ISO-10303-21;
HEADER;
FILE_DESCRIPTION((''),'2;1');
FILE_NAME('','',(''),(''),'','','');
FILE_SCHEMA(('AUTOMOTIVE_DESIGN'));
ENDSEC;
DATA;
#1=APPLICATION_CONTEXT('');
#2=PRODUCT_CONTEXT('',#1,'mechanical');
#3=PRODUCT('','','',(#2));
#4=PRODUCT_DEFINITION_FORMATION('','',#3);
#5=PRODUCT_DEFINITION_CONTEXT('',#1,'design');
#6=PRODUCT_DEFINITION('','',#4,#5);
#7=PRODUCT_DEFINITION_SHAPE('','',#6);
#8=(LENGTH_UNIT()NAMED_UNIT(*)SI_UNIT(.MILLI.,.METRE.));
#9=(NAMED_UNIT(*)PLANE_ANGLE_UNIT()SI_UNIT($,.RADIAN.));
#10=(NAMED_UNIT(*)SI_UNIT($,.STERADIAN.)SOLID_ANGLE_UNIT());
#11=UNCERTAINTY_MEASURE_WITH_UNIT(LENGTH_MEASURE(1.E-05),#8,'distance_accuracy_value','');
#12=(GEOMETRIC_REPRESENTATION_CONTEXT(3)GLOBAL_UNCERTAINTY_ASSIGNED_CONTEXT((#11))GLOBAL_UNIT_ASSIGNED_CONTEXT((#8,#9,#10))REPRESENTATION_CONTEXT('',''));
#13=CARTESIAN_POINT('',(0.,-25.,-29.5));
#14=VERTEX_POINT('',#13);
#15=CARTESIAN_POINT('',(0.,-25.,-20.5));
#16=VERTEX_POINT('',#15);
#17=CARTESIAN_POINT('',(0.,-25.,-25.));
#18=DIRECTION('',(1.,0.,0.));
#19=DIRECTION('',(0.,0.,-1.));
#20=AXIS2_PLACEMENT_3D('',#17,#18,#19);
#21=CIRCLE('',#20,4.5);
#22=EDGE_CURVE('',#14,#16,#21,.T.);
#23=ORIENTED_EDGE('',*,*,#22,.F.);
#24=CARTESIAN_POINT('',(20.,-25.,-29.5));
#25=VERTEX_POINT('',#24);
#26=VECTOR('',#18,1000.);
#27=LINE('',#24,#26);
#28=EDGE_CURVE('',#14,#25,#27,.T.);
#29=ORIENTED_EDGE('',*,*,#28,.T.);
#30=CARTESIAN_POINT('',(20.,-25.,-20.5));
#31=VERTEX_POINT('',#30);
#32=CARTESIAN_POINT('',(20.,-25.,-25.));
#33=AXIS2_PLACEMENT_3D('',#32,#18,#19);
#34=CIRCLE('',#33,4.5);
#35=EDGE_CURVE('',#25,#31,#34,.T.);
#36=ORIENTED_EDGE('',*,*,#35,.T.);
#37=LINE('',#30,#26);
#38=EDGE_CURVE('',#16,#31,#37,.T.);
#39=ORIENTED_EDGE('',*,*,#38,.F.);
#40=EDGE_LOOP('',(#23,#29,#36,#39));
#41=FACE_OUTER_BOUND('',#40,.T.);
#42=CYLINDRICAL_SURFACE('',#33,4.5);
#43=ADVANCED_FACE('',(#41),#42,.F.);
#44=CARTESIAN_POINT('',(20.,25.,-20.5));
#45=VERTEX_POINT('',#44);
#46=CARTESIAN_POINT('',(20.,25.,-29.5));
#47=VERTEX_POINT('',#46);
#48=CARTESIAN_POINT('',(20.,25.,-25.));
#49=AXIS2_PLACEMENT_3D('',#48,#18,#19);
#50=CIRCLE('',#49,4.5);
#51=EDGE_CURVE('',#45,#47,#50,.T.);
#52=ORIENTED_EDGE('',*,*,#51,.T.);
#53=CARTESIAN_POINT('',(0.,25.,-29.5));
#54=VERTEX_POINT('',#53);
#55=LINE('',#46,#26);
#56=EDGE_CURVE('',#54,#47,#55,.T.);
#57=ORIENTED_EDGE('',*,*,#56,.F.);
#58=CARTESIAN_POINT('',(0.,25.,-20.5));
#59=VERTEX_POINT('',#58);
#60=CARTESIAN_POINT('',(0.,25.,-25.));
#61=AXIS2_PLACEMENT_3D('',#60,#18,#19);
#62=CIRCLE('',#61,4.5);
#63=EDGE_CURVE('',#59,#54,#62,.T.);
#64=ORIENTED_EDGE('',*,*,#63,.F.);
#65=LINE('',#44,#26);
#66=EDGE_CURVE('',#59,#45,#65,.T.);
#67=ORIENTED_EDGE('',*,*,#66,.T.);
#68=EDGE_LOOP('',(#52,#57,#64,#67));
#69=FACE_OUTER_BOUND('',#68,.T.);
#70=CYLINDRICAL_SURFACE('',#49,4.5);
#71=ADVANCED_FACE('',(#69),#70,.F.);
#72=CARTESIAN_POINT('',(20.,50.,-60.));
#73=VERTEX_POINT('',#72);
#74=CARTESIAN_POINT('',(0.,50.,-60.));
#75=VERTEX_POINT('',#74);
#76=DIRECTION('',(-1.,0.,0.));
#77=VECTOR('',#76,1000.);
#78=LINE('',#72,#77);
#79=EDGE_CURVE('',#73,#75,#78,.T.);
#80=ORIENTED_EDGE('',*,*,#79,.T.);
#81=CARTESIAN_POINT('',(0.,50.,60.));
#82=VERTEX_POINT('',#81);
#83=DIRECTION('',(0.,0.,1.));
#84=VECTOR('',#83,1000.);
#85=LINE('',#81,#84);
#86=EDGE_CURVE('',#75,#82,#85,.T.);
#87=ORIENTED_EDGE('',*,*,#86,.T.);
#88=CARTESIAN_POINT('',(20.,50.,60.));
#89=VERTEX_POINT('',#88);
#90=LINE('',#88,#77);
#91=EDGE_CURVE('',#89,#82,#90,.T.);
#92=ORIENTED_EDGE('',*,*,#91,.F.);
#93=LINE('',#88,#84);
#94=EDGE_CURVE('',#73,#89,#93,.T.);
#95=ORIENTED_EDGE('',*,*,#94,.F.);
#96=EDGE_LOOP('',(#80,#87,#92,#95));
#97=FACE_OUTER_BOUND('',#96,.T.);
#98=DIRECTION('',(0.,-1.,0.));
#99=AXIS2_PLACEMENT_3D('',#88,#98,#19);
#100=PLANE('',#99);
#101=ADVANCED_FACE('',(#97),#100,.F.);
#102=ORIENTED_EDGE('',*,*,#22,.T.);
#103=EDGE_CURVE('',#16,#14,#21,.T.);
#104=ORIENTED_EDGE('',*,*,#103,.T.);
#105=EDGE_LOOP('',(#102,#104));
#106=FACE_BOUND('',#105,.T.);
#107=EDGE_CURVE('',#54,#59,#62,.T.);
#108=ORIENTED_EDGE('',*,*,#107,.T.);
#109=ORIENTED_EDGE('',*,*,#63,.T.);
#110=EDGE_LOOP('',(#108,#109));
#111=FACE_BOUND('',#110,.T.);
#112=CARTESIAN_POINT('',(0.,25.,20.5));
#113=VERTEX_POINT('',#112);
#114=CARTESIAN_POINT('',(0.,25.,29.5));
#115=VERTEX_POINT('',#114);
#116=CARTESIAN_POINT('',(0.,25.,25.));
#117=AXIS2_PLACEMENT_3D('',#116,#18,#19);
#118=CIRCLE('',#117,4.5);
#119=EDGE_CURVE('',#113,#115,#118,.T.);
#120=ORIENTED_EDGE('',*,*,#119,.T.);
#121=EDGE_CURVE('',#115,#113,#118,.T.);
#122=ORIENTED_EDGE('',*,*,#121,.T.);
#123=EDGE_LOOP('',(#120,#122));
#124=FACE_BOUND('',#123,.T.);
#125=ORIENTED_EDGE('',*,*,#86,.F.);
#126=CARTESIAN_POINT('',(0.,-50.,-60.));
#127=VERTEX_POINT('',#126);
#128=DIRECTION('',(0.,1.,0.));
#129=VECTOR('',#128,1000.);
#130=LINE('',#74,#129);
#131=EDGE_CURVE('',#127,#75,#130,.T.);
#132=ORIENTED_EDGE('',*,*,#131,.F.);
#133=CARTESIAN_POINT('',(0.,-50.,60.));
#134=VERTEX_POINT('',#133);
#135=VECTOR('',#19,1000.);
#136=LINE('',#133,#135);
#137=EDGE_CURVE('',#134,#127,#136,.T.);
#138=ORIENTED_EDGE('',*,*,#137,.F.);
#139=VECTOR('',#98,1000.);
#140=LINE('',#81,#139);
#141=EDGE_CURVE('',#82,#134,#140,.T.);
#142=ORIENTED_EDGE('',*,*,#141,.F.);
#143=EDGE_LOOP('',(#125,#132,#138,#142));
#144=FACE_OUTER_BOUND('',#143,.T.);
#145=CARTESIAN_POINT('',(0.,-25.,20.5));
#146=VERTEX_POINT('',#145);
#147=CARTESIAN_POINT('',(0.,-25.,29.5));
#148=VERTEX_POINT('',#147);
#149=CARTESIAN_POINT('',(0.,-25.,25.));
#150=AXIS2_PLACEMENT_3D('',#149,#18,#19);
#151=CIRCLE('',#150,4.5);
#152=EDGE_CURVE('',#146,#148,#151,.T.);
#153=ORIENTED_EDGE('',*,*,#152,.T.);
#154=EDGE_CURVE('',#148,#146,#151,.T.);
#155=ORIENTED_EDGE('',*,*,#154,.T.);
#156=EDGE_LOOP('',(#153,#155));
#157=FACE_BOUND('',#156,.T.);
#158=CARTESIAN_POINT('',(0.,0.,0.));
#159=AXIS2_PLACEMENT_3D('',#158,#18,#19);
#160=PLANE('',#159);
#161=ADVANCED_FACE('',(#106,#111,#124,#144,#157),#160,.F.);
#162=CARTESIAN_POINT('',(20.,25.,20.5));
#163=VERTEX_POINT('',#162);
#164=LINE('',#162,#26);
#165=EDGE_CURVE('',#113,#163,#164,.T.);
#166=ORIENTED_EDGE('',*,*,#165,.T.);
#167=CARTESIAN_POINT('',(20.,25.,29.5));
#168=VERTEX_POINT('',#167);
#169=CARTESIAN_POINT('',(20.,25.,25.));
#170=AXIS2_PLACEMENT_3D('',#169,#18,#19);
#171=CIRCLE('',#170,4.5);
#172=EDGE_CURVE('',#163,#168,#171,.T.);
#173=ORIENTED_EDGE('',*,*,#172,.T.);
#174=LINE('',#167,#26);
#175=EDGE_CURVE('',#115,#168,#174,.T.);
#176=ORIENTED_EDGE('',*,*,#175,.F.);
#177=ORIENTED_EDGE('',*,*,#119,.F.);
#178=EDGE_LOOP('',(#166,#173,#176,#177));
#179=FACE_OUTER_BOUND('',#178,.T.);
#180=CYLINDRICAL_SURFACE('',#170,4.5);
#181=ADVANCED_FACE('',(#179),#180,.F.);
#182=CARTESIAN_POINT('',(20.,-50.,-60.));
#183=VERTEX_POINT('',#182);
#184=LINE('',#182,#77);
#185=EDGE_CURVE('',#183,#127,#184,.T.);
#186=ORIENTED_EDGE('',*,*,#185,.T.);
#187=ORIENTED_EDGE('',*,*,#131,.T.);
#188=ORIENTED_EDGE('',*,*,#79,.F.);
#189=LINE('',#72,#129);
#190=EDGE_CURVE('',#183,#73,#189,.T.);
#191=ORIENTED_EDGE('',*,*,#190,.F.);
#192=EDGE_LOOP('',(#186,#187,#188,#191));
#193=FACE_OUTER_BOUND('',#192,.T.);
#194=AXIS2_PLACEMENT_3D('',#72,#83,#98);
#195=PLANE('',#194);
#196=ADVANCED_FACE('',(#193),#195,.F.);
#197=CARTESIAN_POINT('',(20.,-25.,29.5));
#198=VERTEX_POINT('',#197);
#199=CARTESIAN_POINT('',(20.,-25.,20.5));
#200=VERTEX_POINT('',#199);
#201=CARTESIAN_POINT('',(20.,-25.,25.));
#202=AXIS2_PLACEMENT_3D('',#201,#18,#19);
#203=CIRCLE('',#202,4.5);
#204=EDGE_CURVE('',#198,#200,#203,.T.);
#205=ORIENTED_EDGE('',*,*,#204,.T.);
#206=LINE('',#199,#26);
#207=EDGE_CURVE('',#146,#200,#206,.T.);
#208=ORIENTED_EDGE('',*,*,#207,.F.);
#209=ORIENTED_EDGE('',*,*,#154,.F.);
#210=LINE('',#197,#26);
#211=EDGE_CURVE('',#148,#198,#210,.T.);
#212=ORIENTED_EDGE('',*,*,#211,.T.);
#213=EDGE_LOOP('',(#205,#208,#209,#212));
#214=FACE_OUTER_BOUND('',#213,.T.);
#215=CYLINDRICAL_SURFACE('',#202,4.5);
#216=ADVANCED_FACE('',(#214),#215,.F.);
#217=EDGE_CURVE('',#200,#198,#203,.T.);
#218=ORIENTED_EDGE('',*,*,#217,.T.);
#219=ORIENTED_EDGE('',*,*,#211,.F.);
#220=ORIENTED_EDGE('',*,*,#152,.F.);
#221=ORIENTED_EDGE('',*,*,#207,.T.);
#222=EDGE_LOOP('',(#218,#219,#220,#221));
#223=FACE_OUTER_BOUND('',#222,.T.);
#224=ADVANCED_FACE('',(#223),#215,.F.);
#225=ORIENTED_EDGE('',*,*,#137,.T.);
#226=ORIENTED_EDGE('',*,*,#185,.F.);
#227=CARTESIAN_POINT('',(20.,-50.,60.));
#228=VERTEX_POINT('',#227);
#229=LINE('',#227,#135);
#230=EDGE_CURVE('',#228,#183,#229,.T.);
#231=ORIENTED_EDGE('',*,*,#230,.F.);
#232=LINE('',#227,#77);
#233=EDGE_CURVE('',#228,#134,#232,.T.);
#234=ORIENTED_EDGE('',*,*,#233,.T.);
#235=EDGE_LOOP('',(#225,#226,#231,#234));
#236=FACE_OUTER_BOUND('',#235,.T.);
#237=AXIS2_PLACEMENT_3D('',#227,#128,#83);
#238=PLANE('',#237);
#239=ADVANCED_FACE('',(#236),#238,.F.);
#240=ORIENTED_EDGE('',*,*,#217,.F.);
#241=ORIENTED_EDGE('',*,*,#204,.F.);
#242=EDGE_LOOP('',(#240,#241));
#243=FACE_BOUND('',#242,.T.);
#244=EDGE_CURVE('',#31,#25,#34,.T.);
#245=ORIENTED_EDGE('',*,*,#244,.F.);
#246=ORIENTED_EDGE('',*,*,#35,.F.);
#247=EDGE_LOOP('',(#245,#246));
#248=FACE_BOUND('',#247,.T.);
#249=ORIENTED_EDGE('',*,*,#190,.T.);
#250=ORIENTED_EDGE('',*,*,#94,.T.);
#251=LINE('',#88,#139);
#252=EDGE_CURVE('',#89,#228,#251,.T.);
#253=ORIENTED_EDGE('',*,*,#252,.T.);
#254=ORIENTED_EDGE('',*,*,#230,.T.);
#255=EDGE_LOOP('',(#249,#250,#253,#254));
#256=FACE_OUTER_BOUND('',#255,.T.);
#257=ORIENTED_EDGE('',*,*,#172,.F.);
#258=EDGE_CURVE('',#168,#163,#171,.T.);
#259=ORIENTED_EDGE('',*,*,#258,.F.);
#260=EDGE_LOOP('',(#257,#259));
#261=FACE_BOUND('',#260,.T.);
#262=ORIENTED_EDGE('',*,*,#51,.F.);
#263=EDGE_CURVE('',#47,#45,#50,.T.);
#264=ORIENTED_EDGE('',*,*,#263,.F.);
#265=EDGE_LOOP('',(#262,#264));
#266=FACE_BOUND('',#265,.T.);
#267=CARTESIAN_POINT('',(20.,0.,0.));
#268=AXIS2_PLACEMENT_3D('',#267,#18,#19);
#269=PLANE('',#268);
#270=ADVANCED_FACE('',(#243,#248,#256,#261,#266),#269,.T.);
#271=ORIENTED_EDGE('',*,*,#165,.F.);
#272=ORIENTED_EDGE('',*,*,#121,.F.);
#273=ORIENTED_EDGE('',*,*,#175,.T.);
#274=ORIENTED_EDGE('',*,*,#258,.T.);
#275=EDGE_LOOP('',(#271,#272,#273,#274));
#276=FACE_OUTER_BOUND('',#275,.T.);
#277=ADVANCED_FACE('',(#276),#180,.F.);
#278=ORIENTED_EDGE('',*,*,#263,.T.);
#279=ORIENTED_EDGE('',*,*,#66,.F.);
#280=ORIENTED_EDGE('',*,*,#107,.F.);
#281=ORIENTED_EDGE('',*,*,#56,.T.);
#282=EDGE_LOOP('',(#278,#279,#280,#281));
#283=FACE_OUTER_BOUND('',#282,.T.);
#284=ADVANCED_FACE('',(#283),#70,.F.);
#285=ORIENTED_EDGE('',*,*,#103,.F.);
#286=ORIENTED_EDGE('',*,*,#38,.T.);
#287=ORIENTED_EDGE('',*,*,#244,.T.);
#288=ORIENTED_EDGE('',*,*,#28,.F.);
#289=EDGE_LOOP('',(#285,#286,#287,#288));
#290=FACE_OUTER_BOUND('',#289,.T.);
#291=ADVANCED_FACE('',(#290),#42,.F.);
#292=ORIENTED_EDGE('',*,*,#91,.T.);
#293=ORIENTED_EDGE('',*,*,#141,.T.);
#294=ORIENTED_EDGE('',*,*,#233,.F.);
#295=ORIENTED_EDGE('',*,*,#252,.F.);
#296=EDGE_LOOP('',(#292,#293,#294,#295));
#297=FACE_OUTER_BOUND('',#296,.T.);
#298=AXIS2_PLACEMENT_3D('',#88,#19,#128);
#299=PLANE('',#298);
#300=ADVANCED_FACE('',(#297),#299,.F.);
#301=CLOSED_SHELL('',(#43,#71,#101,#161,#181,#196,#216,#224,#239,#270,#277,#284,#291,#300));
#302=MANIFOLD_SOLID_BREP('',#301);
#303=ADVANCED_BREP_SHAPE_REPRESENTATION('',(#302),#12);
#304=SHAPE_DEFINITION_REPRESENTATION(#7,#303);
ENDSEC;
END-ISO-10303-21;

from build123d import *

# Parameters (mm, degrees)
SKETCH_1_W            = 120
SKETCH_1_H            = 100
EXTRUDE_1_DEPTH       = 20
HOLE_WIZARD_9_0_9_1_D = 9


with BuildPart() as part:
    # 草图1 → 凸台-拉伸1 (new body)
    with BuildSketch(Plane(origin=(0, 0, 0), x_dir=(0, 0, -1), z_dir=(1, 0, 0))):
        Rectangle(SKETCH_1_W, SKETCH_1_H)
    extrude(amount=EXTRUDE_1_DEPTH)

    # Ø9.0 (9) 直径孔1 (through all)
    with Locations(Plane(origin=(20, 0, 0), x_dir=(0, 0, -1), z_dir=(1, 0, 0))):
        with Locations((-25, 25), (25, 25), (-25, -25), (25, -25)):
            Hole(HOLE_WIZARD_9_0_9_1_D / 2)


solid = part.part
